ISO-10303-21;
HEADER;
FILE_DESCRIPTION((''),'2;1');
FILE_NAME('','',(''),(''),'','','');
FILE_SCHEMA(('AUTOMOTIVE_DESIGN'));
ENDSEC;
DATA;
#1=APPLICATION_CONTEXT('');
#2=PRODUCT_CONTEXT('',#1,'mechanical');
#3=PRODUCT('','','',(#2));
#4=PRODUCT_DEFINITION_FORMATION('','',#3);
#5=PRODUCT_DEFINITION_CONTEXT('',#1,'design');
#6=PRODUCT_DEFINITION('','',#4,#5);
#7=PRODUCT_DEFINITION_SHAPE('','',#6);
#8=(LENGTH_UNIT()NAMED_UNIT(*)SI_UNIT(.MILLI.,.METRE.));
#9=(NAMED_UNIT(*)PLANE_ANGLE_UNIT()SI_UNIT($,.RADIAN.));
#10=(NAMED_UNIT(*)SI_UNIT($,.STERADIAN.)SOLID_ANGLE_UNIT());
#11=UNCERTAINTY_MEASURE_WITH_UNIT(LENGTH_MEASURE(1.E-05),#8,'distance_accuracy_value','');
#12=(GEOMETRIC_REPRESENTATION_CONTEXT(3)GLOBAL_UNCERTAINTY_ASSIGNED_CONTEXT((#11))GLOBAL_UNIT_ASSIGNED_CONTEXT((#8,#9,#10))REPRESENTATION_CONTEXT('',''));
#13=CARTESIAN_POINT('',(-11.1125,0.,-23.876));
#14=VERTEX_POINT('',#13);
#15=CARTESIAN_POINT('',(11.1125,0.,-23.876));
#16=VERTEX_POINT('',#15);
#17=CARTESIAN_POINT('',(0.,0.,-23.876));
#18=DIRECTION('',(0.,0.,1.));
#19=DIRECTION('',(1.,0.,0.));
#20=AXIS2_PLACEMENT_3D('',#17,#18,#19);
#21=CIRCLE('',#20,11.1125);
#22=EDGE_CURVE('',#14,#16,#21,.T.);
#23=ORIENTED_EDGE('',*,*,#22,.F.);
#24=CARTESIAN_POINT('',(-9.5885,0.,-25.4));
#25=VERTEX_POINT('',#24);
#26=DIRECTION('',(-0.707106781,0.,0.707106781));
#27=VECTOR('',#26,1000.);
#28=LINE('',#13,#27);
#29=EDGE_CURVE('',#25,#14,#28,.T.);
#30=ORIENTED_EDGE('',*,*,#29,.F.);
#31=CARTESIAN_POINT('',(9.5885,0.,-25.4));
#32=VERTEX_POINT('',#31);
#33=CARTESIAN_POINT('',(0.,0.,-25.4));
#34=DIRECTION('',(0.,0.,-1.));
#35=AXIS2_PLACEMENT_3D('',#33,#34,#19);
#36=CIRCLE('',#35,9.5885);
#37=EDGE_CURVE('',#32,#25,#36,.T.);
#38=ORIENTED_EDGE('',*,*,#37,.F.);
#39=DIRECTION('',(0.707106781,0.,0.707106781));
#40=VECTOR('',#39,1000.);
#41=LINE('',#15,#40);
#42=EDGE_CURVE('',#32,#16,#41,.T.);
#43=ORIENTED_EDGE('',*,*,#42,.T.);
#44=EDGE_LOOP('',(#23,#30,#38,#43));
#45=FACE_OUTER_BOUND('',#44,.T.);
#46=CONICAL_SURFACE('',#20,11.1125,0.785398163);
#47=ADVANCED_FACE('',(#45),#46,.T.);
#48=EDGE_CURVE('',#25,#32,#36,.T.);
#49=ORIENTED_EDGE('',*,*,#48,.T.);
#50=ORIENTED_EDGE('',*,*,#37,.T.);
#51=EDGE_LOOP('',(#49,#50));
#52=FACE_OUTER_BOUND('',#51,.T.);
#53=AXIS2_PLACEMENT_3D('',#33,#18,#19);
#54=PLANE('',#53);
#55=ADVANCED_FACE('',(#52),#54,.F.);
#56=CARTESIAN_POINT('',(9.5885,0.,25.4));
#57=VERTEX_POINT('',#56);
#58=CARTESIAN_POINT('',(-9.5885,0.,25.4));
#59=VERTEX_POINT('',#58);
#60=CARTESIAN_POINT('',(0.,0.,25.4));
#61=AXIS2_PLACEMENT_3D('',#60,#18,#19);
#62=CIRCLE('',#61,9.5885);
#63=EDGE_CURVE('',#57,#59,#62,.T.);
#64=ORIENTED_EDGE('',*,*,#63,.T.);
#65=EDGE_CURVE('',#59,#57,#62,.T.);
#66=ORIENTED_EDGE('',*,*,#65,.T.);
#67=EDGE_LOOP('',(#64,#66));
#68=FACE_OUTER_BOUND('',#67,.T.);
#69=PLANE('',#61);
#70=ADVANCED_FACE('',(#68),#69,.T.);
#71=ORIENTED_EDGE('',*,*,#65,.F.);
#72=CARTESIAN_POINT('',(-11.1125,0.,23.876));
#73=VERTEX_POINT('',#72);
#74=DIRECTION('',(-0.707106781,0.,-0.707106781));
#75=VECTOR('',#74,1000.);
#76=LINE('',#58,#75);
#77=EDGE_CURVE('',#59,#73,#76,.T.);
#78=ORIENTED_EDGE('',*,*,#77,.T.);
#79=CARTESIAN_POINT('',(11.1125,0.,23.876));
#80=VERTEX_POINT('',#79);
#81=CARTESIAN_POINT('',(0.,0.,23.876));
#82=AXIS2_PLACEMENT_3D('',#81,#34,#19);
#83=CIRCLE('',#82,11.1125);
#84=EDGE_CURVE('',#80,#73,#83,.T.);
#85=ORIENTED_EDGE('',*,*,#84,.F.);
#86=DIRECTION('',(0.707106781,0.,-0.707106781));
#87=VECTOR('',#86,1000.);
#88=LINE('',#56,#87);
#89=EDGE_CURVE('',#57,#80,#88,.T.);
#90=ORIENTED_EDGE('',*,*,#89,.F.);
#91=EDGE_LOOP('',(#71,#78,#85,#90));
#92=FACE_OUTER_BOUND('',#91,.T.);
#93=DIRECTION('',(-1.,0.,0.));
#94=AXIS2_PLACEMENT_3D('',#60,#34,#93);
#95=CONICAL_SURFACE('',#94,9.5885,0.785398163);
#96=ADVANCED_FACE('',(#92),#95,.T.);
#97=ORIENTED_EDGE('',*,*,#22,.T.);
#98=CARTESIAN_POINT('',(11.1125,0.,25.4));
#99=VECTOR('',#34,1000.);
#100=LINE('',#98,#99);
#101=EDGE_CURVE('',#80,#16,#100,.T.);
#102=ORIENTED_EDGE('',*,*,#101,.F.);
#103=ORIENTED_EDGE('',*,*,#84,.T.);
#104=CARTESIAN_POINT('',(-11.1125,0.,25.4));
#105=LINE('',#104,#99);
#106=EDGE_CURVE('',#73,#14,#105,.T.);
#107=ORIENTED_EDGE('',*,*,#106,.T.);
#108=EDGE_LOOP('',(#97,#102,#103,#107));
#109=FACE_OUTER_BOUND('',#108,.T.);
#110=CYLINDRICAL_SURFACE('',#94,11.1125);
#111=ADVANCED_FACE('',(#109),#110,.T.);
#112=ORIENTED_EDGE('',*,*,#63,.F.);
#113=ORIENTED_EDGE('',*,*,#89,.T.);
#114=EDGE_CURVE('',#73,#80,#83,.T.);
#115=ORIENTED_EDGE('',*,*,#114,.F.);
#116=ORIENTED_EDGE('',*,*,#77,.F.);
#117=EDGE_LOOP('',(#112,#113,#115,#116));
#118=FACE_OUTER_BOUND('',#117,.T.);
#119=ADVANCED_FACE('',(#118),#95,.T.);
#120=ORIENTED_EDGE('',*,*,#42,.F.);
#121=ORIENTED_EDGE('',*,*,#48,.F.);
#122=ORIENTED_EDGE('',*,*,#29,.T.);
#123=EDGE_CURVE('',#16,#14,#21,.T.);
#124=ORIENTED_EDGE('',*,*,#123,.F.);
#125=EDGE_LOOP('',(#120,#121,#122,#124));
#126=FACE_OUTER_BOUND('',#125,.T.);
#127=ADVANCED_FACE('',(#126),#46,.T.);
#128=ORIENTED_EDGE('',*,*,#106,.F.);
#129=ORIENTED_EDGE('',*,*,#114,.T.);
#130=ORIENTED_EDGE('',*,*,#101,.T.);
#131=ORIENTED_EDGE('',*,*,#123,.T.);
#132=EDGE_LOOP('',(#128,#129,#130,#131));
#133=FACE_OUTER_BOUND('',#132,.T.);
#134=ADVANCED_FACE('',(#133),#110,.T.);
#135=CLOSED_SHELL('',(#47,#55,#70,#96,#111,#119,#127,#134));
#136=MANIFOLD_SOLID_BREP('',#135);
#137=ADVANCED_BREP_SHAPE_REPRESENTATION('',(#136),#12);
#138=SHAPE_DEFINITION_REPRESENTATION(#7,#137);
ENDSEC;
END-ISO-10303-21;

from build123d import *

# Parameters (mm, degrees)
SKETCH1_R      = 11.1125
EXTRUDE1_DEPTH = 25.4
CHAMFER1_SIZE  = 1.524


with BuildPart() as part:
    # Sketch1 → Extrude1 (new, symmetric)
    with BuildSketch(Plane.XY):
        Circle(SKETCH1_R)
    extrude(amount=EXTRUDE1_DEPTH, both=True)

    # Chamfer1
    chamfer1_edges = [part.edges().sort_by_distance(p)[0] for p in [
        (-11.1125, 0, -25.4),
        (-11.1125, 0, 25.4),
    ]]
    chamfer(chamfer1_edges, length=CHAMFER1_SIZE)


solid = part.part
